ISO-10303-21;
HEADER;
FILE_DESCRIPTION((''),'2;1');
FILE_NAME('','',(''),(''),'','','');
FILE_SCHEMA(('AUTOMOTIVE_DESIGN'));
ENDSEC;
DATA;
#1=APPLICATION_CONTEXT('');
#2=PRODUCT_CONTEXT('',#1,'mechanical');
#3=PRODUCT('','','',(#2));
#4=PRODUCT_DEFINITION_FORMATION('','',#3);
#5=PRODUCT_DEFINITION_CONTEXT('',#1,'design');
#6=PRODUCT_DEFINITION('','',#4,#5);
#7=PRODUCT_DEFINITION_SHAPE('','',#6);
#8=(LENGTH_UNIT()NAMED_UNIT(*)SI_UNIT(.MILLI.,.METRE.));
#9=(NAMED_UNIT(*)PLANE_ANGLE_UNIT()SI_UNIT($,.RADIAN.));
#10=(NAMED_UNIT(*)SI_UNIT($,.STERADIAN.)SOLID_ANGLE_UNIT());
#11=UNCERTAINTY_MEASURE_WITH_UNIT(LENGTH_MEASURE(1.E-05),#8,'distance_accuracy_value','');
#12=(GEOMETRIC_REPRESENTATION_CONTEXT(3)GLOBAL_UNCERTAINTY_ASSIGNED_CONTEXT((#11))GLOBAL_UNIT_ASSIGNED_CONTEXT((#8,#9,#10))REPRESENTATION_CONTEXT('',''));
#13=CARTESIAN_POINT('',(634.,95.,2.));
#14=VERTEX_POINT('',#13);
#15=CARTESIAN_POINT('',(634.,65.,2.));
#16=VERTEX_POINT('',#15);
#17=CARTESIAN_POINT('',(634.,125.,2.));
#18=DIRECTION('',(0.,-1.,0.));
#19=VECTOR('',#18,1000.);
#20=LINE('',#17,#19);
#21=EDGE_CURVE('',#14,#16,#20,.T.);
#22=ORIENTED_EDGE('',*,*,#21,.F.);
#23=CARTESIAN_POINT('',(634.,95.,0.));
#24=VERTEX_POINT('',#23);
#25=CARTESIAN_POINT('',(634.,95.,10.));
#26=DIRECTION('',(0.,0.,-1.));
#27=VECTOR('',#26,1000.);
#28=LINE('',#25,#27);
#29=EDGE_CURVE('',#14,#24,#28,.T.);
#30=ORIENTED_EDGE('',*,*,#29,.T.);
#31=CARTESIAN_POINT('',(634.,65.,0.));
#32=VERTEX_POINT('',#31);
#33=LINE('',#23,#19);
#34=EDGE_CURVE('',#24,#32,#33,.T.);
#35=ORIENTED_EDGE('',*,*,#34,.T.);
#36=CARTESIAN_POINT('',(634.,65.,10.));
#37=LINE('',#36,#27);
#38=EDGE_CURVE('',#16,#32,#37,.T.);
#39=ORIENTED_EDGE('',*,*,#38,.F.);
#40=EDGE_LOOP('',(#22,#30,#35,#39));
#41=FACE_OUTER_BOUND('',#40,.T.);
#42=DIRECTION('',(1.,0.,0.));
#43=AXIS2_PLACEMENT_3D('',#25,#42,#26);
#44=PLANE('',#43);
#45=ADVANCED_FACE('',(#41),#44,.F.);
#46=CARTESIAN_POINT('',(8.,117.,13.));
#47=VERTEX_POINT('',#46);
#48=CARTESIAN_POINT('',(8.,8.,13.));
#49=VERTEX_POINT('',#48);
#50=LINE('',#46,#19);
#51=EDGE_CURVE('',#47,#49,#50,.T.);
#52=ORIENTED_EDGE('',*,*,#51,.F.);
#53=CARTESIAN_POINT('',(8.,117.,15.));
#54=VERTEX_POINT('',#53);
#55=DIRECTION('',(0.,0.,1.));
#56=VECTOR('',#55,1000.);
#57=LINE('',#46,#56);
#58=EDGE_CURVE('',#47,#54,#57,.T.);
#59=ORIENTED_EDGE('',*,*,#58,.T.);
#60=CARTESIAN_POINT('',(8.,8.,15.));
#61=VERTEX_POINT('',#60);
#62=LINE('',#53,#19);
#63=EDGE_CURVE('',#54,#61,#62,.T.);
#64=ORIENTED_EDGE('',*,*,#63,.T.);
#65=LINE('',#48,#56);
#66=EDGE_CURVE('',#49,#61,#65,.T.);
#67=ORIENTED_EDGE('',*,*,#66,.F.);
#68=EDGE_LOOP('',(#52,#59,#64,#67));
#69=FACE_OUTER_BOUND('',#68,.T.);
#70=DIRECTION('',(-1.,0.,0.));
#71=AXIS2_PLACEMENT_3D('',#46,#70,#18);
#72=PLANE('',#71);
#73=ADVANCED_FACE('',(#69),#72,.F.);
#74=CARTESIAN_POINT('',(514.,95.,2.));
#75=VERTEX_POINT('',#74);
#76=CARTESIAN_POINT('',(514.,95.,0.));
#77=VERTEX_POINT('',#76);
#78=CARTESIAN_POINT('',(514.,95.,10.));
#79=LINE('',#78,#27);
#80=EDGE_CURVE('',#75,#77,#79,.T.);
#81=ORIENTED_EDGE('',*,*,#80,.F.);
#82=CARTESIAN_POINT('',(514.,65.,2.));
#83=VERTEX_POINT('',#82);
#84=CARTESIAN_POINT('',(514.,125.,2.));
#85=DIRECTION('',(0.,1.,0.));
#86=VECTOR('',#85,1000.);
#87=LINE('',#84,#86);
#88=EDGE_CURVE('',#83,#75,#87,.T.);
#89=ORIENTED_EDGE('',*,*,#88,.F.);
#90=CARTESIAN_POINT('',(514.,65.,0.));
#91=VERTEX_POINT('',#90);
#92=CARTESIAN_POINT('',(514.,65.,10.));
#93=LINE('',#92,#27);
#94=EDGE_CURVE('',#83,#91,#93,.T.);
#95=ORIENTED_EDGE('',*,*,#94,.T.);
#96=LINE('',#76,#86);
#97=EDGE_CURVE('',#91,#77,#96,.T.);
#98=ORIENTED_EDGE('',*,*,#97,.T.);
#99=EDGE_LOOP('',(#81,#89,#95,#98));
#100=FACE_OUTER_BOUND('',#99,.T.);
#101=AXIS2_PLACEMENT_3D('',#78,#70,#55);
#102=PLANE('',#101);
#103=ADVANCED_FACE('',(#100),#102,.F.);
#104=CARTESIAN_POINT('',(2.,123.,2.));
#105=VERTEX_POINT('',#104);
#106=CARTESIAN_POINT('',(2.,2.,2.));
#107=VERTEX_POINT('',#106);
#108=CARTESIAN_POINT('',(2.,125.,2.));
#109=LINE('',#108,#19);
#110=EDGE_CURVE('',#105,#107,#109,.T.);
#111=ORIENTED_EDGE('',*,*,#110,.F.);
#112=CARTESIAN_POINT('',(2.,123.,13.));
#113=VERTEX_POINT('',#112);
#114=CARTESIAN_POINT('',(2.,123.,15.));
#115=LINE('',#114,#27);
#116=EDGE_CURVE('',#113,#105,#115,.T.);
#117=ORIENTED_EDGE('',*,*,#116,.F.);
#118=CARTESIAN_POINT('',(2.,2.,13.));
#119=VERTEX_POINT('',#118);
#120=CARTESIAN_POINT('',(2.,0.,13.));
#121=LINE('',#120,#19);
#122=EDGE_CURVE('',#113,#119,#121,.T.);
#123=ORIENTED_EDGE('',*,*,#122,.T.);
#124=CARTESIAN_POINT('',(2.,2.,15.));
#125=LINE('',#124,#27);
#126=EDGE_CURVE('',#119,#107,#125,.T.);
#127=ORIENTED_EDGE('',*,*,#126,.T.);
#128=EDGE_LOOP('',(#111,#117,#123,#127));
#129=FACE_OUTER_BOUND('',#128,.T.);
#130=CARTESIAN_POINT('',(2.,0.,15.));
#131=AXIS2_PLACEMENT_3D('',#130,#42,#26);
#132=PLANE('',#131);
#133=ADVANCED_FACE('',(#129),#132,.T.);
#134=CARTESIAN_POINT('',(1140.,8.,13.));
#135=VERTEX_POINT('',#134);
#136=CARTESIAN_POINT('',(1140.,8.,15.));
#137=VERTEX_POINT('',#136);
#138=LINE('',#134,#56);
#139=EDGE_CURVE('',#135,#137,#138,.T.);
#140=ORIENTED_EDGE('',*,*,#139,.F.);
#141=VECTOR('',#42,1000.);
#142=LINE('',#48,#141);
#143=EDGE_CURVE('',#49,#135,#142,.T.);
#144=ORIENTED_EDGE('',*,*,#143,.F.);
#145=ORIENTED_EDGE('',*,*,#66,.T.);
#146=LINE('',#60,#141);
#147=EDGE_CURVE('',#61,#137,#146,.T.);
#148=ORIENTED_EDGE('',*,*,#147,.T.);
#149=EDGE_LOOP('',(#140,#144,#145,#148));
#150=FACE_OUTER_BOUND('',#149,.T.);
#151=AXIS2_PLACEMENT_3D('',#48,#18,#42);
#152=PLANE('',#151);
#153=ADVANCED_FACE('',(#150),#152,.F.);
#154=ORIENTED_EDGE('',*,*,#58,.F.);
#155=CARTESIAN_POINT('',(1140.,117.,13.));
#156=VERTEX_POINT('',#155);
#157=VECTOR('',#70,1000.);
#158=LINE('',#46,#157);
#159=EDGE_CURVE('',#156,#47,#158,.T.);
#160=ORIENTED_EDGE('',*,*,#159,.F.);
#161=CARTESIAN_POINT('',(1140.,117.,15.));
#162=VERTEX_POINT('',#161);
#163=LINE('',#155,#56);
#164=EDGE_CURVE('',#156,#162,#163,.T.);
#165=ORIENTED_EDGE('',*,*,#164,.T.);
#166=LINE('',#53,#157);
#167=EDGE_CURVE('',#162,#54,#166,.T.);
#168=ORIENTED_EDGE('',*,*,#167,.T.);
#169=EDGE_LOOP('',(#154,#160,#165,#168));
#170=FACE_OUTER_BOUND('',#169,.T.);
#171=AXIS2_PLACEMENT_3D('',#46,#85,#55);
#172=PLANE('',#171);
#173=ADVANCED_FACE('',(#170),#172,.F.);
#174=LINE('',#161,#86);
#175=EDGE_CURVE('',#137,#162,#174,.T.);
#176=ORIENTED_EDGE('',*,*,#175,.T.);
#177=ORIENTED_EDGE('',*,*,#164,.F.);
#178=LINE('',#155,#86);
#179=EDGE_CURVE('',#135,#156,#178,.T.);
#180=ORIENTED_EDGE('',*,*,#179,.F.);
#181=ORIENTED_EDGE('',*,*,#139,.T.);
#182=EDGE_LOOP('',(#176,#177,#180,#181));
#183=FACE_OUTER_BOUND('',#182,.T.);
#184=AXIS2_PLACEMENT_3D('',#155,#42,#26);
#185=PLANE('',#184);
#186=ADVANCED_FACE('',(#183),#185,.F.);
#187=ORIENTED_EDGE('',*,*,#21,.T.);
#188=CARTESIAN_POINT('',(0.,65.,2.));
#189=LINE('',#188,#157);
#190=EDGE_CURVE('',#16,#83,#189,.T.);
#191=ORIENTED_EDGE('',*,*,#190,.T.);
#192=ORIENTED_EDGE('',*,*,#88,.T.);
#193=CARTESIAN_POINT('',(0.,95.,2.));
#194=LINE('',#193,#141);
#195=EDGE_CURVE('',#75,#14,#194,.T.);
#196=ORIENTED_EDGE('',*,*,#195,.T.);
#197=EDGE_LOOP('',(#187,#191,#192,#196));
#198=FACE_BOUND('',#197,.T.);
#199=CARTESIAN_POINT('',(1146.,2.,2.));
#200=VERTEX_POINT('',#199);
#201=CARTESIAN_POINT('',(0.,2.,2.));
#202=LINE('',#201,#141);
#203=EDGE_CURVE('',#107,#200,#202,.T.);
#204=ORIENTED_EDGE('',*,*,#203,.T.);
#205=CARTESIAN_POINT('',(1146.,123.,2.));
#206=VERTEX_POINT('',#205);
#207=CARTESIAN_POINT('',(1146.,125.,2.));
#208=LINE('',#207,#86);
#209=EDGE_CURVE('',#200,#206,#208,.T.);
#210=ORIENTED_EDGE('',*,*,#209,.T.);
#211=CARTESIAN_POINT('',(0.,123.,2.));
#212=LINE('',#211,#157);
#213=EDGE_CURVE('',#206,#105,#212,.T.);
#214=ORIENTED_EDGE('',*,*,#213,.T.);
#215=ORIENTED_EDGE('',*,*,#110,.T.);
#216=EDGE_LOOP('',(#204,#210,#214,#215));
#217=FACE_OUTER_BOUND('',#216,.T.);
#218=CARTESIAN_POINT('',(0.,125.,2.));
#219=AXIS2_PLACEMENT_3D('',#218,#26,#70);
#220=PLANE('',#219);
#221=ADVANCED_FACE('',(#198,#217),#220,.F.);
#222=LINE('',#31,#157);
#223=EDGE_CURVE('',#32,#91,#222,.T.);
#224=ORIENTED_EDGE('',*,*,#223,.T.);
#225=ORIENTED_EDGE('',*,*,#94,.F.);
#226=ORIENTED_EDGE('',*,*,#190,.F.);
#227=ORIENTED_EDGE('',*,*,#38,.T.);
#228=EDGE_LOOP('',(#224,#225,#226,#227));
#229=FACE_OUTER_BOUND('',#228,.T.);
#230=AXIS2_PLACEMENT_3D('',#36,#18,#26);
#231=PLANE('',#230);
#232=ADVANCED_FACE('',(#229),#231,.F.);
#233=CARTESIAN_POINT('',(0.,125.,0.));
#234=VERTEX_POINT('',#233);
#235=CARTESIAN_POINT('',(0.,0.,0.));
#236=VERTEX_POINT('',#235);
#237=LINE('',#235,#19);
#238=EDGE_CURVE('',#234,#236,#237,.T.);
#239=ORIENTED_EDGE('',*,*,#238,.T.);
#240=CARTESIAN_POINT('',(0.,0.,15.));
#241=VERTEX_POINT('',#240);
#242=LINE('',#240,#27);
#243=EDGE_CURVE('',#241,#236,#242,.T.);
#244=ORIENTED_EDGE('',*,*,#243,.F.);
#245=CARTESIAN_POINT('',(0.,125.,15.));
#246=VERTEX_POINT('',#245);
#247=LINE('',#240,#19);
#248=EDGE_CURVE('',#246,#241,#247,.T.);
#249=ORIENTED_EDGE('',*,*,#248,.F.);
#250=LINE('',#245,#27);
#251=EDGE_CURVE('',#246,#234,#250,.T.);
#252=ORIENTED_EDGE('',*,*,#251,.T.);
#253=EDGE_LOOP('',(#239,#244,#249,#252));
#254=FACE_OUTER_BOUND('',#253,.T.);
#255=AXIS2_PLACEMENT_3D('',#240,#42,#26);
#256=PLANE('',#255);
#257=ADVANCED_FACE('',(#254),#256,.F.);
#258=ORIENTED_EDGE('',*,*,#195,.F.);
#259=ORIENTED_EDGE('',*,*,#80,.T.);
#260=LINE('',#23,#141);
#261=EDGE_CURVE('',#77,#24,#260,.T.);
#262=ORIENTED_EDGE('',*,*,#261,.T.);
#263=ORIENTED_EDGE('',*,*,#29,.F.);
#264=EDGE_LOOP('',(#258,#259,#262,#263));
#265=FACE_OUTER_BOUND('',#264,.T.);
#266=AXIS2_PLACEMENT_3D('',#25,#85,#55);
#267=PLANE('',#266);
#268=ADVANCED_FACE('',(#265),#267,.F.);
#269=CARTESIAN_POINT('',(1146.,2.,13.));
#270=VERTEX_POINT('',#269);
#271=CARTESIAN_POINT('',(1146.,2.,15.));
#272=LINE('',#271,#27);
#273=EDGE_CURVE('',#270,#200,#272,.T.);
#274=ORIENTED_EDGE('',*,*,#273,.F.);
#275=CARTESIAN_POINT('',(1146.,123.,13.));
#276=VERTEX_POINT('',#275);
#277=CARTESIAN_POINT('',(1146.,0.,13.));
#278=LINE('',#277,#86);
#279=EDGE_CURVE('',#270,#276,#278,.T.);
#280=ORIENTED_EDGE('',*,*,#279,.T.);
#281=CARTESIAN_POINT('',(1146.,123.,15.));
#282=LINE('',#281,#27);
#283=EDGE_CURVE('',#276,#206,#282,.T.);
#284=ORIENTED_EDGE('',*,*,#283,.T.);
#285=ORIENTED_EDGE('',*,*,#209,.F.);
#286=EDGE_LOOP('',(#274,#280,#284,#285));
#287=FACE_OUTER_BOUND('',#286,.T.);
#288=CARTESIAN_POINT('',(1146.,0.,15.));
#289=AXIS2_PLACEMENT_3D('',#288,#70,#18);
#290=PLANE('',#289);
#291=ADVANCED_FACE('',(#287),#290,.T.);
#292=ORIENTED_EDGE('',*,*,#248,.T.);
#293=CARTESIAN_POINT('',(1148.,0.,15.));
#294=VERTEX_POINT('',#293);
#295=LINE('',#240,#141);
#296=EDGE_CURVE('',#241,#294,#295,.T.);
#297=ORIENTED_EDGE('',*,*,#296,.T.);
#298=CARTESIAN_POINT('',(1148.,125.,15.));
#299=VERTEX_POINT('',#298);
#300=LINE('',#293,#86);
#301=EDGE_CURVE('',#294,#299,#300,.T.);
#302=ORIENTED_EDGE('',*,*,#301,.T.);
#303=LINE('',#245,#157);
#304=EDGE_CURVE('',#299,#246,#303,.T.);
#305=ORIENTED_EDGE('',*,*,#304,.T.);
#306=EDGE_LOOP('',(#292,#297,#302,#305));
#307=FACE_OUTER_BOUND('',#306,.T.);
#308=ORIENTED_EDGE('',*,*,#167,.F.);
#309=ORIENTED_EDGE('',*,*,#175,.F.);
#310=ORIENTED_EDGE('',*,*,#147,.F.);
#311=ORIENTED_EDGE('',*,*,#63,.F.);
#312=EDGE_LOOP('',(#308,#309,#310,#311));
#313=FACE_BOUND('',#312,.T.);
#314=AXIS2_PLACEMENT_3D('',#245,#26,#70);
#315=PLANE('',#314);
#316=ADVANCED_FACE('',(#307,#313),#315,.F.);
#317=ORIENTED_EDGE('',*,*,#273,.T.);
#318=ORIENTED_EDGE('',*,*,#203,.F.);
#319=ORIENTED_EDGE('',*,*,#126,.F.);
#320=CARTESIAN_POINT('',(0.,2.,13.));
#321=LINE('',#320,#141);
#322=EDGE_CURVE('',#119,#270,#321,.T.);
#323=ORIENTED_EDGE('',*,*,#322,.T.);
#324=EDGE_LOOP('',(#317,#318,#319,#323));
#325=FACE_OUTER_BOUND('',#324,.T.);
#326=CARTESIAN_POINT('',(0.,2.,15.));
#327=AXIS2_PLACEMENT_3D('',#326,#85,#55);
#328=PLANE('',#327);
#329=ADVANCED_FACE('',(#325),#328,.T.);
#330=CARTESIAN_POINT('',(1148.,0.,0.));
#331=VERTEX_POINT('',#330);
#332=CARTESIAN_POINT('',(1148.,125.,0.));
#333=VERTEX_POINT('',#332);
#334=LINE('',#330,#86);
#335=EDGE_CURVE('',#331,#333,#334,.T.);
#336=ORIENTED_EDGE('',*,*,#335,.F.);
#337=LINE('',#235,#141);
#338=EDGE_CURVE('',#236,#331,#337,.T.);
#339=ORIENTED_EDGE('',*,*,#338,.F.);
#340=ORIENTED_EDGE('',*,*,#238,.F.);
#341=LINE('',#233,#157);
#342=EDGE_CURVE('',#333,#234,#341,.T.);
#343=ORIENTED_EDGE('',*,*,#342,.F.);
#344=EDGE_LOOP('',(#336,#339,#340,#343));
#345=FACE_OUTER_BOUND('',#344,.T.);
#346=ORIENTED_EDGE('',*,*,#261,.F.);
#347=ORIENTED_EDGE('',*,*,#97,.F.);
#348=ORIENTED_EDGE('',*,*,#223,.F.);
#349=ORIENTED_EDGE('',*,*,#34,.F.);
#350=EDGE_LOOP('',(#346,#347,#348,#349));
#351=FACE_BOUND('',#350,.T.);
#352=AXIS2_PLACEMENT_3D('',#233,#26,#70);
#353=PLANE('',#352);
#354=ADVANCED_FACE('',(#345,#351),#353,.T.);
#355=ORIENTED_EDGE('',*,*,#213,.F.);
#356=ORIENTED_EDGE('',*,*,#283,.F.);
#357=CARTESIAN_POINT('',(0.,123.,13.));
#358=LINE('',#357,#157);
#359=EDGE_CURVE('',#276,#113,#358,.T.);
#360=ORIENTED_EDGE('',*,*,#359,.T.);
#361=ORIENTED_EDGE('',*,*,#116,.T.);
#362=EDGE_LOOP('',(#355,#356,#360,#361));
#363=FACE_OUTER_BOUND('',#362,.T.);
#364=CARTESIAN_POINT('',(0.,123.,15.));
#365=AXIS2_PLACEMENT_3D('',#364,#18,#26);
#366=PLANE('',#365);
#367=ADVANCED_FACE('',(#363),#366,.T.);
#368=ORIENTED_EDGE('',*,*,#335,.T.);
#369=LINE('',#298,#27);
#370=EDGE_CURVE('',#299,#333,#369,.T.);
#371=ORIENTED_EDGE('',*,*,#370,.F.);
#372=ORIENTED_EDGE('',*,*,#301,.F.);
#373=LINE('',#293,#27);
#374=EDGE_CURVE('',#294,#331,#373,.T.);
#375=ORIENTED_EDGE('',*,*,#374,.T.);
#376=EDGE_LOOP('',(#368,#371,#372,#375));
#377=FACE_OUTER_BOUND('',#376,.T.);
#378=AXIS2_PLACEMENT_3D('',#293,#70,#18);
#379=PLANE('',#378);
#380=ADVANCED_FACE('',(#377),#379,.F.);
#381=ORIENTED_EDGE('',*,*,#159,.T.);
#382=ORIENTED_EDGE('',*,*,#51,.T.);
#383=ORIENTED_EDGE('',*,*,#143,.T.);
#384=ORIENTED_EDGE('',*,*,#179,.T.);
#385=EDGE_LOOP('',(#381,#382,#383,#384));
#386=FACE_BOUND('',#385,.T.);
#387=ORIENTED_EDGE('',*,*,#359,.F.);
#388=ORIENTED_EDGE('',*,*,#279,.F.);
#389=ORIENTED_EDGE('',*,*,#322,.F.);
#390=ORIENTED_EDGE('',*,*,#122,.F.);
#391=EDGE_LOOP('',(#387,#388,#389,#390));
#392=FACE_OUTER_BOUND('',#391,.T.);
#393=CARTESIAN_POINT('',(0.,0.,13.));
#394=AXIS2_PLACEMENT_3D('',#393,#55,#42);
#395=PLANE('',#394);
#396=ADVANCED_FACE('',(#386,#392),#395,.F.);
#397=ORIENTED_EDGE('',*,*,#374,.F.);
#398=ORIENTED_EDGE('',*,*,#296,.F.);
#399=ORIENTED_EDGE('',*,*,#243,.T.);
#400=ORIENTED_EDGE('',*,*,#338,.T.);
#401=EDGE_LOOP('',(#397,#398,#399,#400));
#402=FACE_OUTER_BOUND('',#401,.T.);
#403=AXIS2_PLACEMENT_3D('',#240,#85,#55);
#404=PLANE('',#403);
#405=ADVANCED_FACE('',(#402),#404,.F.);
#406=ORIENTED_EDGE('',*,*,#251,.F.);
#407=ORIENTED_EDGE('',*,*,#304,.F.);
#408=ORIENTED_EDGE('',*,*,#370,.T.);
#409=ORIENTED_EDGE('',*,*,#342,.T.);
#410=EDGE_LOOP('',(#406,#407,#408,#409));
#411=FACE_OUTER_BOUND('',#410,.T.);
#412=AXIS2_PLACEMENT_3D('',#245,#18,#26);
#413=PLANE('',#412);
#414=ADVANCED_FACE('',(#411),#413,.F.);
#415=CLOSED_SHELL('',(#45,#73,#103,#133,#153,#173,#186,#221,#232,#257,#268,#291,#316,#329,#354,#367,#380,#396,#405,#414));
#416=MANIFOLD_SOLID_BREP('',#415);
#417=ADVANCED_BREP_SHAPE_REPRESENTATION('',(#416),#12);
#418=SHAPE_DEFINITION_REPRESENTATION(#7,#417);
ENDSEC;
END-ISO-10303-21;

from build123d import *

# Parameters (mm, degrees)
SKETCH_1_W          = 1148
SKETCH_1_H          = 125
EXTRUDE_1_DEPTH     = 15
SHELL_1_T           = -2
SKETCH_2_W          = 1148
SKETCH_2_H          = 125
SKETCH_2_W_2        = 1132
SKETCH_2_H_2        = 109
EXTRUDE_2_DEPTH     = 2
SKETCH_3_W          = 120
SKETCH_3_H          = 30
CUT_EXTRUDE_1_DEPTH = 10


with BuildPart() as part:
    # 草图1 → 凸台-拉伸1 (new body)
    with BuildSketch(Plane.XY):
        with Locations((574, 62.5)):
            Rectangle(SKETCH_1_W, SKETCH_1_H)
    extrude(amount=EXTRUDE_1_DEPTH)

    # 抽壳1
    shell_1_openings = [part.faces().sort_by_distance(p)[0] for p in [
        (574, 62.5, 15),
    ]]
    offset(amount=SHELL_1_T, openings=shell_1_openings, kind=Kind.INTERSECTION)

    # 草图2 → 凸台-拉伸2 (add)
    with BuildSketch(Plane.XY.offset(15)):
        with Locations((574, 62.5)):
            Rectangle(SKETCH_2_W, SKETCH_2_H)
        with Locations((574, 62.5)):
            Rectangle(SKETCH_2_W_2, SKETCH_2_H_2, mode=Mode.SUBTRACT)
    extrude(amount=-EXTRUDE_2_DEPTH)

    # 草图3 → 切除-拉伸1 (cut)
    with BuildSketch(Plane(origin=(0, 0, 0), x_dir=(-1, 0, 0), z_dir=(0, 0, -1))):
        with Locations((-574, 80)):
            Rectangle(SKETCH_3_W, SKETCH_3_H)
    extrude(amount=-CUT_EXTRUDE_1_DEPTH, mode=Mode.SUBTRACT)


solid = part.part
